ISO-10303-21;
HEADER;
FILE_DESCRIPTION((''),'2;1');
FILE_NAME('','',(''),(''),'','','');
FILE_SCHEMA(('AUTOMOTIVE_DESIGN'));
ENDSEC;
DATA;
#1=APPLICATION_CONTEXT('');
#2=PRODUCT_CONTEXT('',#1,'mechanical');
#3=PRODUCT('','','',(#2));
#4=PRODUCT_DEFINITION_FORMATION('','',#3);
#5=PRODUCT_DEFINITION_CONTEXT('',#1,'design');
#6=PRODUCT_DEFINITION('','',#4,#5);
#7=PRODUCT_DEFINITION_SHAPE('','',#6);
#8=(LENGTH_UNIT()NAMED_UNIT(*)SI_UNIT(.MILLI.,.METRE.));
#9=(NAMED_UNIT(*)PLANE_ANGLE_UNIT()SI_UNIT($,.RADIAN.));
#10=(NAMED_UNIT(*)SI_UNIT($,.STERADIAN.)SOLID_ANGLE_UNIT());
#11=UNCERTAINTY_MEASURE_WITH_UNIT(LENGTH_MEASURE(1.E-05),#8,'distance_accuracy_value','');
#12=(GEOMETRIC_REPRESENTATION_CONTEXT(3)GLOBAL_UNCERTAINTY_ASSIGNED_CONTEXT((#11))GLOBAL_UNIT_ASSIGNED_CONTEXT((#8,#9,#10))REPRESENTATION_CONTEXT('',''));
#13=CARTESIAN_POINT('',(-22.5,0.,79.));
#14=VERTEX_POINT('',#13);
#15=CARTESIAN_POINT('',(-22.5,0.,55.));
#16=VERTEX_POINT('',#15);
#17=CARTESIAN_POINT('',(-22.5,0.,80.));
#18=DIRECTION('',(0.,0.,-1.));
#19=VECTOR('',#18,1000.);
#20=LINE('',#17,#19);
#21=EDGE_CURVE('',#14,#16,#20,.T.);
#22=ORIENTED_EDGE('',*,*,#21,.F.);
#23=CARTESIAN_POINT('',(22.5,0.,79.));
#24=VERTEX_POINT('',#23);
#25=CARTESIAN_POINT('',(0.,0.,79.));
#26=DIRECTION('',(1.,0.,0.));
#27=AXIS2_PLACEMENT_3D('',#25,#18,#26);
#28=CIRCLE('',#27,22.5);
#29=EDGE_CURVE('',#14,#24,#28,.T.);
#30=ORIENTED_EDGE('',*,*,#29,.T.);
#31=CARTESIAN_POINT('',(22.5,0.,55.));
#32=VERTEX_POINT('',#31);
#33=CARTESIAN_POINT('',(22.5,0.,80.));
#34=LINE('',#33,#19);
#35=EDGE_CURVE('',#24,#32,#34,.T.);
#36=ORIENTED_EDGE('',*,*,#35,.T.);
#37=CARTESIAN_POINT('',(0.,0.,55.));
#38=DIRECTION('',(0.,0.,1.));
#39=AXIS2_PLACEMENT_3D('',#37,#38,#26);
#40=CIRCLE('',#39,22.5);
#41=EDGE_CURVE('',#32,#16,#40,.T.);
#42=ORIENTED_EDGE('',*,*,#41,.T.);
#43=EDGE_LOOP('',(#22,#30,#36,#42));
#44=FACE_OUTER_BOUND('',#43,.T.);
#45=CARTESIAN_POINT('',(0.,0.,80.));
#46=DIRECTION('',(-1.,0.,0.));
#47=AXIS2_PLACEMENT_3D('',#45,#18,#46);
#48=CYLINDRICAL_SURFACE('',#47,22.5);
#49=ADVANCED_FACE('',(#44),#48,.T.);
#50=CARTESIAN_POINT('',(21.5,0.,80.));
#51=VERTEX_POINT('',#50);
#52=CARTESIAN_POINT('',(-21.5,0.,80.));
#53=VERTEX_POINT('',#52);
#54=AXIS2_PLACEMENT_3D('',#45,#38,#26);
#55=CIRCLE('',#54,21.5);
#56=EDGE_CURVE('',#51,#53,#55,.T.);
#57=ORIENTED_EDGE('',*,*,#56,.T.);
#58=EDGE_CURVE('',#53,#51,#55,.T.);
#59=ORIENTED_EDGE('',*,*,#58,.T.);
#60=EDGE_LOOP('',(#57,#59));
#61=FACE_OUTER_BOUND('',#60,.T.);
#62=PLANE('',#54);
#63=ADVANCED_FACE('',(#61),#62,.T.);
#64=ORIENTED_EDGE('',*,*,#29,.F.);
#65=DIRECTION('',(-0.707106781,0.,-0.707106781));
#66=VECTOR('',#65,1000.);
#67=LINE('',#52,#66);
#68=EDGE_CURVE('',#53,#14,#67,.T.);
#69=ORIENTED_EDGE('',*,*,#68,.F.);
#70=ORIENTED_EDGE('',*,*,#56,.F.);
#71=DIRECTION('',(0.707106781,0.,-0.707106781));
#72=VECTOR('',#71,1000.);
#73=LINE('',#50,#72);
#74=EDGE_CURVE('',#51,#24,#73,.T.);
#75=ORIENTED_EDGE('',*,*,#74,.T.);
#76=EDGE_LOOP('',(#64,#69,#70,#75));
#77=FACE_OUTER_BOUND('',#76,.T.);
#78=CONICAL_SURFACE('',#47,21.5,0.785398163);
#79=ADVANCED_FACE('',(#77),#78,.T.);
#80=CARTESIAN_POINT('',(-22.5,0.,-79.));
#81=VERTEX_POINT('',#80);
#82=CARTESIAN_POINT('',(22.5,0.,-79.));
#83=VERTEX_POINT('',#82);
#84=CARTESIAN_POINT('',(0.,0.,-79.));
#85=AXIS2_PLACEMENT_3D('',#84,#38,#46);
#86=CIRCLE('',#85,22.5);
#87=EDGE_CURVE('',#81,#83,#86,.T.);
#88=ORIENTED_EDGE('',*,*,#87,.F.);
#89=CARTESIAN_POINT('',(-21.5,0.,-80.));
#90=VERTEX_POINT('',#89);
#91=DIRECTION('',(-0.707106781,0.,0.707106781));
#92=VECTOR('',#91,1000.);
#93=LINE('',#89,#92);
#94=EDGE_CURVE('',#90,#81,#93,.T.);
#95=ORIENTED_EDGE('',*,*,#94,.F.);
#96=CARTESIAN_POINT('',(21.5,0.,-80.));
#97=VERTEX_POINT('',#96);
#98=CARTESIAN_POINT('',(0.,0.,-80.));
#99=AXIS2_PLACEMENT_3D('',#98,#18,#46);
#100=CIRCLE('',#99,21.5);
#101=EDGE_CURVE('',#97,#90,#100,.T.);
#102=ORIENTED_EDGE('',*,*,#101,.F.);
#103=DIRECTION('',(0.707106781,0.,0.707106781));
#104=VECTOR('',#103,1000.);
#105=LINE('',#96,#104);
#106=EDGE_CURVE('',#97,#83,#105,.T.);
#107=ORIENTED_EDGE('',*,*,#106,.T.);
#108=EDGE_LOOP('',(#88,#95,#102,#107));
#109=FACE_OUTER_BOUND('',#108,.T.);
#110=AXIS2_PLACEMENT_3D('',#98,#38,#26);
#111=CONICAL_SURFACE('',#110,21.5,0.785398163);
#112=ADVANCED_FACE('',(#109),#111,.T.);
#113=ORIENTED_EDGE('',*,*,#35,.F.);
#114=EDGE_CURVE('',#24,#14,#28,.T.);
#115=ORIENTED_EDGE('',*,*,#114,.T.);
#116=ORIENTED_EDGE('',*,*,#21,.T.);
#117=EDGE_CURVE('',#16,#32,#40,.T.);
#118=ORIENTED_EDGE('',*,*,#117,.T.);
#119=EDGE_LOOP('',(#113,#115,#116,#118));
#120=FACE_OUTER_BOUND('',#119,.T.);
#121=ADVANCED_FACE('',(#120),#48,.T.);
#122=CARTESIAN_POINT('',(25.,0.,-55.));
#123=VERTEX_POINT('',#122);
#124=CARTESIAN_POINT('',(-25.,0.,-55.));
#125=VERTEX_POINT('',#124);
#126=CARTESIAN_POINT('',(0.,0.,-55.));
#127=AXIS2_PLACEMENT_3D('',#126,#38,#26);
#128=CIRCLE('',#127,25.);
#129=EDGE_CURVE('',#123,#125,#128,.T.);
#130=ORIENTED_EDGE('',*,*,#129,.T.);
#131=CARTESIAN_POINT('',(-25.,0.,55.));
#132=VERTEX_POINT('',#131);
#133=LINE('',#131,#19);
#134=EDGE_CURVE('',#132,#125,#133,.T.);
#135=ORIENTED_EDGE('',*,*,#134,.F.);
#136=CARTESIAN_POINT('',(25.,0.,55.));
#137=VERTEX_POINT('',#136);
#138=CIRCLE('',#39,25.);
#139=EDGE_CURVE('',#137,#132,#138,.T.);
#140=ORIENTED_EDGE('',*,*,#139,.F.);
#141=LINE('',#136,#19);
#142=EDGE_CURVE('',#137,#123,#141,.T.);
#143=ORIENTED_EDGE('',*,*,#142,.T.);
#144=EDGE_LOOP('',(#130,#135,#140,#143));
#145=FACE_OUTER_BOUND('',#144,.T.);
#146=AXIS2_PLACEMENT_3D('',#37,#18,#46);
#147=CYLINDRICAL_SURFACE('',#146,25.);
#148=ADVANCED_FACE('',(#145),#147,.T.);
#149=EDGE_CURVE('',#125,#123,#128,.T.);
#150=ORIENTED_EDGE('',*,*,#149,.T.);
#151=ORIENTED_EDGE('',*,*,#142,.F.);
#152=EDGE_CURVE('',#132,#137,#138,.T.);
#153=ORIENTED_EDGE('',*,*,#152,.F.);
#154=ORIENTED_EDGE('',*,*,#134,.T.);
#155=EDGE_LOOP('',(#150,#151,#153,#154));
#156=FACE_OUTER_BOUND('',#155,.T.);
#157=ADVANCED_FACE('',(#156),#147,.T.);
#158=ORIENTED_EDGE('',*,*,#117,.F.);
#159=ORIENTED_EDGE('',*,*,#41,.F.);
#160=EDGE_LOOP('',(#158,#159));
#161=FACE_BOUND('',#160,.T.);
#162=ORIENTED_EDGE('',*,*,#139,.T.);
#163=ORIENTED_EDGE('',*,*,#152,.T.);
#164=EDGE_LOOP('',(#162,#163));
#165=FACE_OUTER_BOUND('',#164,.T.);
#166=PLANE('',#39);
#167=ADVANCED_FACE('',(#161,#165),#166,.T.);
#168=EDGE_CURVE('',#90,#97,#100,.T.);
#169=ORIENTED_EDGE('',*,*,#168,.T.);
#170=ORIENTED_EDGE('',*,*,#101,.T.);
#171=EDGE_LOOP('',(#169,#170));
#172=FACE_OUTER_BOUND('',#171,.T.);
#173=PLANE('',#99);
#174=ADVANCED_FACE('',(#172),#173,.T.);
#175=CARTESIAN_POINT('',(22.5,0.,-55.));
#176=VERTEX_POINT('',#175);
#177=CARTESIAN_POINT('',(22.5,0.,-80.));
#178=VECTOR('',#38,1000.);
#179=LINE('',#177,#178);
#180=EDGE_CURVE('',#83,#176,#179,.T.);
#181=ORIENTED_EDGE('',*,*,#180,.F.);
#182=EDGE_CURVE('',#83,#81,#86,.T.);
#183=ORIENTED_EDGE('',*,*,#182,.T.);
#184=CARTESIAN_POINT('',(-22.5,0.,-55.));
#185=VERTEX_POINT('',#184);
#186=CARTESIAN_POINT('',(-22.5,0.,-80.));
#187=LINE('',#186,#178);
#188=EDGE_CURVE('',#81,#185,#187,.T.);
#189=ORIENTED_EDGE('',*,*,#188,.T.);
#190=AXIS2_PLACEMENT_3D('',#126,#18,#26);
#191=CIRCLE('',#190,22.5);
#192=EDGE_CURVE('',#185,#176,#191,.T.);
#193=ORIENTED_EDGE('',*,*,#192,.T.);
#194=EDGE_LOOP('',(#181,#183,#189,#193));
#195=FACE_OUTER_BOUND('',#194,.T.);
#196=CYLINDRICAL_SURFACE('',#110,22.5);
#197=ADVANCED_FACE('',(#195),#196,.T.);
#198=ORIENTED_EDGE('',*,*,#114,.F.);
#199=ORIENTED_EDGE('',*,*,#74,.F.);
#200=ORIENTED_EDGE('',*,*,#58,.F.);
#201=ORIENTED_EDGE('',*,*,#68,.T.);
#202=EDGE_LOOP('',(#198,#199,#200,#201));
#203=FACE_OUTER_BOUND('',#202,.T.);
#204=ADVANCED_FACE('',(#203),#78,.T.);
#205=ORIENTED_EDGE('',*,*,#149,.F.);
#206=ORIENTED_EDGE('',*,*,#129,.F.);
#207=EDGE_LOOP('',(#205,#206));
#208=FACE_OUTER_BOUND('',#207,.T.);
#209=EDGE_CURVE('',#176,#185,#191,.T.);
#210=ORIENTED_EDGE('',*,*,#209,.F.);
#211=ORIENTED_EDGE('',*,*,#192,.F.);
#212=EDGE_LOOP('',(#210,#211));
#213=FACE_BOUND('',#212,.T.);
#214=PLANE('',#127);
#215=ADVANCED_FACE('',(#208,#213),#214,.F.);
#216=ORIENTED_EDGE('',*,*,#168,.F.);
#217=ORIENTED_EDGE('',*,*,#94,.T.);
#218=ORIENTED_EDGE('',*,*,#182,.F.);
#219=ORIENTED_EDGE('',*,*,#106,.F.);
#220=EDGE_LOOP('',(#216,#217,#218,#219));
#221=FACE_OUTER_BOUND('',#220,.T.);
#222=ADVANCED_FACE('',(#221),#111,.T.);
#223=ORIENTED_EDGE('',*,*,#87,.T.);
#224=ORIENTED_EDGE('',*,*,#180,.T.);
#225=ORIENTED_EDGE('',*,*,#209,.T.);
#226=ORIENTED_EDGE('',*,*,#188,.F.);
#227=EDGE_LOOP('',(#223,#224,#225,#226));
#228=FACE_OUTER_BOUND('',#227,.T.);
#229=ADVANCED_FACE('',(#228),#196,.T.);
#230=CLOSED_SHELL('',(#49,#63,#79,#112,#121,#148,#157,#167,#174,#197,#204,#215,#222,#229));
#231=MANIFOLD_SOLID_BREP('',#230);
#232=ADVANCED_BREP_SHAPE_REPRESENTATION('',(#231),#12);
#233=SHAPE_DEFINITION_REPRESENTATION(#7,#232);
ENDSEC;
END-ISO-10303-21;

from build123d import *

# Parameters (mm, degrees)
SKETCH_1_R      = 25
EXTRUDE_1_DEPTH = 55
SKETCH_2_R      = 22.5
EXTRUDE_2_DEPTH = 25
EXTRUDE_START   = 25
SKETCH_3_R      = 22.5
EXTRUDE_3_DEPTH = 25
CHAMFER_1_SIZE  = 1


with BuildPart() as part:
    # 草图1 → 凸台-拉伸1 (new, symmetric)
    with BuildSketch(Plane.XY):
        Circle(SKETCH_1_R)
    extrude(amount=EXTRUDE_1_DEPTH, both=True)

    # 草图2 → 凸台-拉伸2 (add)
    with BuildSketch(Plane.XY.offset(55)):
        Circle(SKETCH_2_R)
    extrude(amount=EXTRUDE_2_DEPTH)

    # 草图3 → 凸台-拉伸3 (add)
    with BuildSketch(Plane(origin=(0, 0, -55), x_dir=(-1, 0, 0), z_dir=(0, 0, -1)).offset(EXTRUDE_START)):
        with Locations(Location((0, 0, 0), (0, 0, 180))):
            Circle(SKETCH_3_R)
    extrude(amount=-EXTRUDE_3_DEPTH)

    # 倒角1
    chamfer_1_edges = [part.edges().sort_by_distance(p)[0] for p in [
        (-22.5, 0, -80),
        (-22.5, 0, 80),
    ]]
    chamfer(chamfer_1_edges, length=CHAMFER_1_SIZE)


solid = part.part
